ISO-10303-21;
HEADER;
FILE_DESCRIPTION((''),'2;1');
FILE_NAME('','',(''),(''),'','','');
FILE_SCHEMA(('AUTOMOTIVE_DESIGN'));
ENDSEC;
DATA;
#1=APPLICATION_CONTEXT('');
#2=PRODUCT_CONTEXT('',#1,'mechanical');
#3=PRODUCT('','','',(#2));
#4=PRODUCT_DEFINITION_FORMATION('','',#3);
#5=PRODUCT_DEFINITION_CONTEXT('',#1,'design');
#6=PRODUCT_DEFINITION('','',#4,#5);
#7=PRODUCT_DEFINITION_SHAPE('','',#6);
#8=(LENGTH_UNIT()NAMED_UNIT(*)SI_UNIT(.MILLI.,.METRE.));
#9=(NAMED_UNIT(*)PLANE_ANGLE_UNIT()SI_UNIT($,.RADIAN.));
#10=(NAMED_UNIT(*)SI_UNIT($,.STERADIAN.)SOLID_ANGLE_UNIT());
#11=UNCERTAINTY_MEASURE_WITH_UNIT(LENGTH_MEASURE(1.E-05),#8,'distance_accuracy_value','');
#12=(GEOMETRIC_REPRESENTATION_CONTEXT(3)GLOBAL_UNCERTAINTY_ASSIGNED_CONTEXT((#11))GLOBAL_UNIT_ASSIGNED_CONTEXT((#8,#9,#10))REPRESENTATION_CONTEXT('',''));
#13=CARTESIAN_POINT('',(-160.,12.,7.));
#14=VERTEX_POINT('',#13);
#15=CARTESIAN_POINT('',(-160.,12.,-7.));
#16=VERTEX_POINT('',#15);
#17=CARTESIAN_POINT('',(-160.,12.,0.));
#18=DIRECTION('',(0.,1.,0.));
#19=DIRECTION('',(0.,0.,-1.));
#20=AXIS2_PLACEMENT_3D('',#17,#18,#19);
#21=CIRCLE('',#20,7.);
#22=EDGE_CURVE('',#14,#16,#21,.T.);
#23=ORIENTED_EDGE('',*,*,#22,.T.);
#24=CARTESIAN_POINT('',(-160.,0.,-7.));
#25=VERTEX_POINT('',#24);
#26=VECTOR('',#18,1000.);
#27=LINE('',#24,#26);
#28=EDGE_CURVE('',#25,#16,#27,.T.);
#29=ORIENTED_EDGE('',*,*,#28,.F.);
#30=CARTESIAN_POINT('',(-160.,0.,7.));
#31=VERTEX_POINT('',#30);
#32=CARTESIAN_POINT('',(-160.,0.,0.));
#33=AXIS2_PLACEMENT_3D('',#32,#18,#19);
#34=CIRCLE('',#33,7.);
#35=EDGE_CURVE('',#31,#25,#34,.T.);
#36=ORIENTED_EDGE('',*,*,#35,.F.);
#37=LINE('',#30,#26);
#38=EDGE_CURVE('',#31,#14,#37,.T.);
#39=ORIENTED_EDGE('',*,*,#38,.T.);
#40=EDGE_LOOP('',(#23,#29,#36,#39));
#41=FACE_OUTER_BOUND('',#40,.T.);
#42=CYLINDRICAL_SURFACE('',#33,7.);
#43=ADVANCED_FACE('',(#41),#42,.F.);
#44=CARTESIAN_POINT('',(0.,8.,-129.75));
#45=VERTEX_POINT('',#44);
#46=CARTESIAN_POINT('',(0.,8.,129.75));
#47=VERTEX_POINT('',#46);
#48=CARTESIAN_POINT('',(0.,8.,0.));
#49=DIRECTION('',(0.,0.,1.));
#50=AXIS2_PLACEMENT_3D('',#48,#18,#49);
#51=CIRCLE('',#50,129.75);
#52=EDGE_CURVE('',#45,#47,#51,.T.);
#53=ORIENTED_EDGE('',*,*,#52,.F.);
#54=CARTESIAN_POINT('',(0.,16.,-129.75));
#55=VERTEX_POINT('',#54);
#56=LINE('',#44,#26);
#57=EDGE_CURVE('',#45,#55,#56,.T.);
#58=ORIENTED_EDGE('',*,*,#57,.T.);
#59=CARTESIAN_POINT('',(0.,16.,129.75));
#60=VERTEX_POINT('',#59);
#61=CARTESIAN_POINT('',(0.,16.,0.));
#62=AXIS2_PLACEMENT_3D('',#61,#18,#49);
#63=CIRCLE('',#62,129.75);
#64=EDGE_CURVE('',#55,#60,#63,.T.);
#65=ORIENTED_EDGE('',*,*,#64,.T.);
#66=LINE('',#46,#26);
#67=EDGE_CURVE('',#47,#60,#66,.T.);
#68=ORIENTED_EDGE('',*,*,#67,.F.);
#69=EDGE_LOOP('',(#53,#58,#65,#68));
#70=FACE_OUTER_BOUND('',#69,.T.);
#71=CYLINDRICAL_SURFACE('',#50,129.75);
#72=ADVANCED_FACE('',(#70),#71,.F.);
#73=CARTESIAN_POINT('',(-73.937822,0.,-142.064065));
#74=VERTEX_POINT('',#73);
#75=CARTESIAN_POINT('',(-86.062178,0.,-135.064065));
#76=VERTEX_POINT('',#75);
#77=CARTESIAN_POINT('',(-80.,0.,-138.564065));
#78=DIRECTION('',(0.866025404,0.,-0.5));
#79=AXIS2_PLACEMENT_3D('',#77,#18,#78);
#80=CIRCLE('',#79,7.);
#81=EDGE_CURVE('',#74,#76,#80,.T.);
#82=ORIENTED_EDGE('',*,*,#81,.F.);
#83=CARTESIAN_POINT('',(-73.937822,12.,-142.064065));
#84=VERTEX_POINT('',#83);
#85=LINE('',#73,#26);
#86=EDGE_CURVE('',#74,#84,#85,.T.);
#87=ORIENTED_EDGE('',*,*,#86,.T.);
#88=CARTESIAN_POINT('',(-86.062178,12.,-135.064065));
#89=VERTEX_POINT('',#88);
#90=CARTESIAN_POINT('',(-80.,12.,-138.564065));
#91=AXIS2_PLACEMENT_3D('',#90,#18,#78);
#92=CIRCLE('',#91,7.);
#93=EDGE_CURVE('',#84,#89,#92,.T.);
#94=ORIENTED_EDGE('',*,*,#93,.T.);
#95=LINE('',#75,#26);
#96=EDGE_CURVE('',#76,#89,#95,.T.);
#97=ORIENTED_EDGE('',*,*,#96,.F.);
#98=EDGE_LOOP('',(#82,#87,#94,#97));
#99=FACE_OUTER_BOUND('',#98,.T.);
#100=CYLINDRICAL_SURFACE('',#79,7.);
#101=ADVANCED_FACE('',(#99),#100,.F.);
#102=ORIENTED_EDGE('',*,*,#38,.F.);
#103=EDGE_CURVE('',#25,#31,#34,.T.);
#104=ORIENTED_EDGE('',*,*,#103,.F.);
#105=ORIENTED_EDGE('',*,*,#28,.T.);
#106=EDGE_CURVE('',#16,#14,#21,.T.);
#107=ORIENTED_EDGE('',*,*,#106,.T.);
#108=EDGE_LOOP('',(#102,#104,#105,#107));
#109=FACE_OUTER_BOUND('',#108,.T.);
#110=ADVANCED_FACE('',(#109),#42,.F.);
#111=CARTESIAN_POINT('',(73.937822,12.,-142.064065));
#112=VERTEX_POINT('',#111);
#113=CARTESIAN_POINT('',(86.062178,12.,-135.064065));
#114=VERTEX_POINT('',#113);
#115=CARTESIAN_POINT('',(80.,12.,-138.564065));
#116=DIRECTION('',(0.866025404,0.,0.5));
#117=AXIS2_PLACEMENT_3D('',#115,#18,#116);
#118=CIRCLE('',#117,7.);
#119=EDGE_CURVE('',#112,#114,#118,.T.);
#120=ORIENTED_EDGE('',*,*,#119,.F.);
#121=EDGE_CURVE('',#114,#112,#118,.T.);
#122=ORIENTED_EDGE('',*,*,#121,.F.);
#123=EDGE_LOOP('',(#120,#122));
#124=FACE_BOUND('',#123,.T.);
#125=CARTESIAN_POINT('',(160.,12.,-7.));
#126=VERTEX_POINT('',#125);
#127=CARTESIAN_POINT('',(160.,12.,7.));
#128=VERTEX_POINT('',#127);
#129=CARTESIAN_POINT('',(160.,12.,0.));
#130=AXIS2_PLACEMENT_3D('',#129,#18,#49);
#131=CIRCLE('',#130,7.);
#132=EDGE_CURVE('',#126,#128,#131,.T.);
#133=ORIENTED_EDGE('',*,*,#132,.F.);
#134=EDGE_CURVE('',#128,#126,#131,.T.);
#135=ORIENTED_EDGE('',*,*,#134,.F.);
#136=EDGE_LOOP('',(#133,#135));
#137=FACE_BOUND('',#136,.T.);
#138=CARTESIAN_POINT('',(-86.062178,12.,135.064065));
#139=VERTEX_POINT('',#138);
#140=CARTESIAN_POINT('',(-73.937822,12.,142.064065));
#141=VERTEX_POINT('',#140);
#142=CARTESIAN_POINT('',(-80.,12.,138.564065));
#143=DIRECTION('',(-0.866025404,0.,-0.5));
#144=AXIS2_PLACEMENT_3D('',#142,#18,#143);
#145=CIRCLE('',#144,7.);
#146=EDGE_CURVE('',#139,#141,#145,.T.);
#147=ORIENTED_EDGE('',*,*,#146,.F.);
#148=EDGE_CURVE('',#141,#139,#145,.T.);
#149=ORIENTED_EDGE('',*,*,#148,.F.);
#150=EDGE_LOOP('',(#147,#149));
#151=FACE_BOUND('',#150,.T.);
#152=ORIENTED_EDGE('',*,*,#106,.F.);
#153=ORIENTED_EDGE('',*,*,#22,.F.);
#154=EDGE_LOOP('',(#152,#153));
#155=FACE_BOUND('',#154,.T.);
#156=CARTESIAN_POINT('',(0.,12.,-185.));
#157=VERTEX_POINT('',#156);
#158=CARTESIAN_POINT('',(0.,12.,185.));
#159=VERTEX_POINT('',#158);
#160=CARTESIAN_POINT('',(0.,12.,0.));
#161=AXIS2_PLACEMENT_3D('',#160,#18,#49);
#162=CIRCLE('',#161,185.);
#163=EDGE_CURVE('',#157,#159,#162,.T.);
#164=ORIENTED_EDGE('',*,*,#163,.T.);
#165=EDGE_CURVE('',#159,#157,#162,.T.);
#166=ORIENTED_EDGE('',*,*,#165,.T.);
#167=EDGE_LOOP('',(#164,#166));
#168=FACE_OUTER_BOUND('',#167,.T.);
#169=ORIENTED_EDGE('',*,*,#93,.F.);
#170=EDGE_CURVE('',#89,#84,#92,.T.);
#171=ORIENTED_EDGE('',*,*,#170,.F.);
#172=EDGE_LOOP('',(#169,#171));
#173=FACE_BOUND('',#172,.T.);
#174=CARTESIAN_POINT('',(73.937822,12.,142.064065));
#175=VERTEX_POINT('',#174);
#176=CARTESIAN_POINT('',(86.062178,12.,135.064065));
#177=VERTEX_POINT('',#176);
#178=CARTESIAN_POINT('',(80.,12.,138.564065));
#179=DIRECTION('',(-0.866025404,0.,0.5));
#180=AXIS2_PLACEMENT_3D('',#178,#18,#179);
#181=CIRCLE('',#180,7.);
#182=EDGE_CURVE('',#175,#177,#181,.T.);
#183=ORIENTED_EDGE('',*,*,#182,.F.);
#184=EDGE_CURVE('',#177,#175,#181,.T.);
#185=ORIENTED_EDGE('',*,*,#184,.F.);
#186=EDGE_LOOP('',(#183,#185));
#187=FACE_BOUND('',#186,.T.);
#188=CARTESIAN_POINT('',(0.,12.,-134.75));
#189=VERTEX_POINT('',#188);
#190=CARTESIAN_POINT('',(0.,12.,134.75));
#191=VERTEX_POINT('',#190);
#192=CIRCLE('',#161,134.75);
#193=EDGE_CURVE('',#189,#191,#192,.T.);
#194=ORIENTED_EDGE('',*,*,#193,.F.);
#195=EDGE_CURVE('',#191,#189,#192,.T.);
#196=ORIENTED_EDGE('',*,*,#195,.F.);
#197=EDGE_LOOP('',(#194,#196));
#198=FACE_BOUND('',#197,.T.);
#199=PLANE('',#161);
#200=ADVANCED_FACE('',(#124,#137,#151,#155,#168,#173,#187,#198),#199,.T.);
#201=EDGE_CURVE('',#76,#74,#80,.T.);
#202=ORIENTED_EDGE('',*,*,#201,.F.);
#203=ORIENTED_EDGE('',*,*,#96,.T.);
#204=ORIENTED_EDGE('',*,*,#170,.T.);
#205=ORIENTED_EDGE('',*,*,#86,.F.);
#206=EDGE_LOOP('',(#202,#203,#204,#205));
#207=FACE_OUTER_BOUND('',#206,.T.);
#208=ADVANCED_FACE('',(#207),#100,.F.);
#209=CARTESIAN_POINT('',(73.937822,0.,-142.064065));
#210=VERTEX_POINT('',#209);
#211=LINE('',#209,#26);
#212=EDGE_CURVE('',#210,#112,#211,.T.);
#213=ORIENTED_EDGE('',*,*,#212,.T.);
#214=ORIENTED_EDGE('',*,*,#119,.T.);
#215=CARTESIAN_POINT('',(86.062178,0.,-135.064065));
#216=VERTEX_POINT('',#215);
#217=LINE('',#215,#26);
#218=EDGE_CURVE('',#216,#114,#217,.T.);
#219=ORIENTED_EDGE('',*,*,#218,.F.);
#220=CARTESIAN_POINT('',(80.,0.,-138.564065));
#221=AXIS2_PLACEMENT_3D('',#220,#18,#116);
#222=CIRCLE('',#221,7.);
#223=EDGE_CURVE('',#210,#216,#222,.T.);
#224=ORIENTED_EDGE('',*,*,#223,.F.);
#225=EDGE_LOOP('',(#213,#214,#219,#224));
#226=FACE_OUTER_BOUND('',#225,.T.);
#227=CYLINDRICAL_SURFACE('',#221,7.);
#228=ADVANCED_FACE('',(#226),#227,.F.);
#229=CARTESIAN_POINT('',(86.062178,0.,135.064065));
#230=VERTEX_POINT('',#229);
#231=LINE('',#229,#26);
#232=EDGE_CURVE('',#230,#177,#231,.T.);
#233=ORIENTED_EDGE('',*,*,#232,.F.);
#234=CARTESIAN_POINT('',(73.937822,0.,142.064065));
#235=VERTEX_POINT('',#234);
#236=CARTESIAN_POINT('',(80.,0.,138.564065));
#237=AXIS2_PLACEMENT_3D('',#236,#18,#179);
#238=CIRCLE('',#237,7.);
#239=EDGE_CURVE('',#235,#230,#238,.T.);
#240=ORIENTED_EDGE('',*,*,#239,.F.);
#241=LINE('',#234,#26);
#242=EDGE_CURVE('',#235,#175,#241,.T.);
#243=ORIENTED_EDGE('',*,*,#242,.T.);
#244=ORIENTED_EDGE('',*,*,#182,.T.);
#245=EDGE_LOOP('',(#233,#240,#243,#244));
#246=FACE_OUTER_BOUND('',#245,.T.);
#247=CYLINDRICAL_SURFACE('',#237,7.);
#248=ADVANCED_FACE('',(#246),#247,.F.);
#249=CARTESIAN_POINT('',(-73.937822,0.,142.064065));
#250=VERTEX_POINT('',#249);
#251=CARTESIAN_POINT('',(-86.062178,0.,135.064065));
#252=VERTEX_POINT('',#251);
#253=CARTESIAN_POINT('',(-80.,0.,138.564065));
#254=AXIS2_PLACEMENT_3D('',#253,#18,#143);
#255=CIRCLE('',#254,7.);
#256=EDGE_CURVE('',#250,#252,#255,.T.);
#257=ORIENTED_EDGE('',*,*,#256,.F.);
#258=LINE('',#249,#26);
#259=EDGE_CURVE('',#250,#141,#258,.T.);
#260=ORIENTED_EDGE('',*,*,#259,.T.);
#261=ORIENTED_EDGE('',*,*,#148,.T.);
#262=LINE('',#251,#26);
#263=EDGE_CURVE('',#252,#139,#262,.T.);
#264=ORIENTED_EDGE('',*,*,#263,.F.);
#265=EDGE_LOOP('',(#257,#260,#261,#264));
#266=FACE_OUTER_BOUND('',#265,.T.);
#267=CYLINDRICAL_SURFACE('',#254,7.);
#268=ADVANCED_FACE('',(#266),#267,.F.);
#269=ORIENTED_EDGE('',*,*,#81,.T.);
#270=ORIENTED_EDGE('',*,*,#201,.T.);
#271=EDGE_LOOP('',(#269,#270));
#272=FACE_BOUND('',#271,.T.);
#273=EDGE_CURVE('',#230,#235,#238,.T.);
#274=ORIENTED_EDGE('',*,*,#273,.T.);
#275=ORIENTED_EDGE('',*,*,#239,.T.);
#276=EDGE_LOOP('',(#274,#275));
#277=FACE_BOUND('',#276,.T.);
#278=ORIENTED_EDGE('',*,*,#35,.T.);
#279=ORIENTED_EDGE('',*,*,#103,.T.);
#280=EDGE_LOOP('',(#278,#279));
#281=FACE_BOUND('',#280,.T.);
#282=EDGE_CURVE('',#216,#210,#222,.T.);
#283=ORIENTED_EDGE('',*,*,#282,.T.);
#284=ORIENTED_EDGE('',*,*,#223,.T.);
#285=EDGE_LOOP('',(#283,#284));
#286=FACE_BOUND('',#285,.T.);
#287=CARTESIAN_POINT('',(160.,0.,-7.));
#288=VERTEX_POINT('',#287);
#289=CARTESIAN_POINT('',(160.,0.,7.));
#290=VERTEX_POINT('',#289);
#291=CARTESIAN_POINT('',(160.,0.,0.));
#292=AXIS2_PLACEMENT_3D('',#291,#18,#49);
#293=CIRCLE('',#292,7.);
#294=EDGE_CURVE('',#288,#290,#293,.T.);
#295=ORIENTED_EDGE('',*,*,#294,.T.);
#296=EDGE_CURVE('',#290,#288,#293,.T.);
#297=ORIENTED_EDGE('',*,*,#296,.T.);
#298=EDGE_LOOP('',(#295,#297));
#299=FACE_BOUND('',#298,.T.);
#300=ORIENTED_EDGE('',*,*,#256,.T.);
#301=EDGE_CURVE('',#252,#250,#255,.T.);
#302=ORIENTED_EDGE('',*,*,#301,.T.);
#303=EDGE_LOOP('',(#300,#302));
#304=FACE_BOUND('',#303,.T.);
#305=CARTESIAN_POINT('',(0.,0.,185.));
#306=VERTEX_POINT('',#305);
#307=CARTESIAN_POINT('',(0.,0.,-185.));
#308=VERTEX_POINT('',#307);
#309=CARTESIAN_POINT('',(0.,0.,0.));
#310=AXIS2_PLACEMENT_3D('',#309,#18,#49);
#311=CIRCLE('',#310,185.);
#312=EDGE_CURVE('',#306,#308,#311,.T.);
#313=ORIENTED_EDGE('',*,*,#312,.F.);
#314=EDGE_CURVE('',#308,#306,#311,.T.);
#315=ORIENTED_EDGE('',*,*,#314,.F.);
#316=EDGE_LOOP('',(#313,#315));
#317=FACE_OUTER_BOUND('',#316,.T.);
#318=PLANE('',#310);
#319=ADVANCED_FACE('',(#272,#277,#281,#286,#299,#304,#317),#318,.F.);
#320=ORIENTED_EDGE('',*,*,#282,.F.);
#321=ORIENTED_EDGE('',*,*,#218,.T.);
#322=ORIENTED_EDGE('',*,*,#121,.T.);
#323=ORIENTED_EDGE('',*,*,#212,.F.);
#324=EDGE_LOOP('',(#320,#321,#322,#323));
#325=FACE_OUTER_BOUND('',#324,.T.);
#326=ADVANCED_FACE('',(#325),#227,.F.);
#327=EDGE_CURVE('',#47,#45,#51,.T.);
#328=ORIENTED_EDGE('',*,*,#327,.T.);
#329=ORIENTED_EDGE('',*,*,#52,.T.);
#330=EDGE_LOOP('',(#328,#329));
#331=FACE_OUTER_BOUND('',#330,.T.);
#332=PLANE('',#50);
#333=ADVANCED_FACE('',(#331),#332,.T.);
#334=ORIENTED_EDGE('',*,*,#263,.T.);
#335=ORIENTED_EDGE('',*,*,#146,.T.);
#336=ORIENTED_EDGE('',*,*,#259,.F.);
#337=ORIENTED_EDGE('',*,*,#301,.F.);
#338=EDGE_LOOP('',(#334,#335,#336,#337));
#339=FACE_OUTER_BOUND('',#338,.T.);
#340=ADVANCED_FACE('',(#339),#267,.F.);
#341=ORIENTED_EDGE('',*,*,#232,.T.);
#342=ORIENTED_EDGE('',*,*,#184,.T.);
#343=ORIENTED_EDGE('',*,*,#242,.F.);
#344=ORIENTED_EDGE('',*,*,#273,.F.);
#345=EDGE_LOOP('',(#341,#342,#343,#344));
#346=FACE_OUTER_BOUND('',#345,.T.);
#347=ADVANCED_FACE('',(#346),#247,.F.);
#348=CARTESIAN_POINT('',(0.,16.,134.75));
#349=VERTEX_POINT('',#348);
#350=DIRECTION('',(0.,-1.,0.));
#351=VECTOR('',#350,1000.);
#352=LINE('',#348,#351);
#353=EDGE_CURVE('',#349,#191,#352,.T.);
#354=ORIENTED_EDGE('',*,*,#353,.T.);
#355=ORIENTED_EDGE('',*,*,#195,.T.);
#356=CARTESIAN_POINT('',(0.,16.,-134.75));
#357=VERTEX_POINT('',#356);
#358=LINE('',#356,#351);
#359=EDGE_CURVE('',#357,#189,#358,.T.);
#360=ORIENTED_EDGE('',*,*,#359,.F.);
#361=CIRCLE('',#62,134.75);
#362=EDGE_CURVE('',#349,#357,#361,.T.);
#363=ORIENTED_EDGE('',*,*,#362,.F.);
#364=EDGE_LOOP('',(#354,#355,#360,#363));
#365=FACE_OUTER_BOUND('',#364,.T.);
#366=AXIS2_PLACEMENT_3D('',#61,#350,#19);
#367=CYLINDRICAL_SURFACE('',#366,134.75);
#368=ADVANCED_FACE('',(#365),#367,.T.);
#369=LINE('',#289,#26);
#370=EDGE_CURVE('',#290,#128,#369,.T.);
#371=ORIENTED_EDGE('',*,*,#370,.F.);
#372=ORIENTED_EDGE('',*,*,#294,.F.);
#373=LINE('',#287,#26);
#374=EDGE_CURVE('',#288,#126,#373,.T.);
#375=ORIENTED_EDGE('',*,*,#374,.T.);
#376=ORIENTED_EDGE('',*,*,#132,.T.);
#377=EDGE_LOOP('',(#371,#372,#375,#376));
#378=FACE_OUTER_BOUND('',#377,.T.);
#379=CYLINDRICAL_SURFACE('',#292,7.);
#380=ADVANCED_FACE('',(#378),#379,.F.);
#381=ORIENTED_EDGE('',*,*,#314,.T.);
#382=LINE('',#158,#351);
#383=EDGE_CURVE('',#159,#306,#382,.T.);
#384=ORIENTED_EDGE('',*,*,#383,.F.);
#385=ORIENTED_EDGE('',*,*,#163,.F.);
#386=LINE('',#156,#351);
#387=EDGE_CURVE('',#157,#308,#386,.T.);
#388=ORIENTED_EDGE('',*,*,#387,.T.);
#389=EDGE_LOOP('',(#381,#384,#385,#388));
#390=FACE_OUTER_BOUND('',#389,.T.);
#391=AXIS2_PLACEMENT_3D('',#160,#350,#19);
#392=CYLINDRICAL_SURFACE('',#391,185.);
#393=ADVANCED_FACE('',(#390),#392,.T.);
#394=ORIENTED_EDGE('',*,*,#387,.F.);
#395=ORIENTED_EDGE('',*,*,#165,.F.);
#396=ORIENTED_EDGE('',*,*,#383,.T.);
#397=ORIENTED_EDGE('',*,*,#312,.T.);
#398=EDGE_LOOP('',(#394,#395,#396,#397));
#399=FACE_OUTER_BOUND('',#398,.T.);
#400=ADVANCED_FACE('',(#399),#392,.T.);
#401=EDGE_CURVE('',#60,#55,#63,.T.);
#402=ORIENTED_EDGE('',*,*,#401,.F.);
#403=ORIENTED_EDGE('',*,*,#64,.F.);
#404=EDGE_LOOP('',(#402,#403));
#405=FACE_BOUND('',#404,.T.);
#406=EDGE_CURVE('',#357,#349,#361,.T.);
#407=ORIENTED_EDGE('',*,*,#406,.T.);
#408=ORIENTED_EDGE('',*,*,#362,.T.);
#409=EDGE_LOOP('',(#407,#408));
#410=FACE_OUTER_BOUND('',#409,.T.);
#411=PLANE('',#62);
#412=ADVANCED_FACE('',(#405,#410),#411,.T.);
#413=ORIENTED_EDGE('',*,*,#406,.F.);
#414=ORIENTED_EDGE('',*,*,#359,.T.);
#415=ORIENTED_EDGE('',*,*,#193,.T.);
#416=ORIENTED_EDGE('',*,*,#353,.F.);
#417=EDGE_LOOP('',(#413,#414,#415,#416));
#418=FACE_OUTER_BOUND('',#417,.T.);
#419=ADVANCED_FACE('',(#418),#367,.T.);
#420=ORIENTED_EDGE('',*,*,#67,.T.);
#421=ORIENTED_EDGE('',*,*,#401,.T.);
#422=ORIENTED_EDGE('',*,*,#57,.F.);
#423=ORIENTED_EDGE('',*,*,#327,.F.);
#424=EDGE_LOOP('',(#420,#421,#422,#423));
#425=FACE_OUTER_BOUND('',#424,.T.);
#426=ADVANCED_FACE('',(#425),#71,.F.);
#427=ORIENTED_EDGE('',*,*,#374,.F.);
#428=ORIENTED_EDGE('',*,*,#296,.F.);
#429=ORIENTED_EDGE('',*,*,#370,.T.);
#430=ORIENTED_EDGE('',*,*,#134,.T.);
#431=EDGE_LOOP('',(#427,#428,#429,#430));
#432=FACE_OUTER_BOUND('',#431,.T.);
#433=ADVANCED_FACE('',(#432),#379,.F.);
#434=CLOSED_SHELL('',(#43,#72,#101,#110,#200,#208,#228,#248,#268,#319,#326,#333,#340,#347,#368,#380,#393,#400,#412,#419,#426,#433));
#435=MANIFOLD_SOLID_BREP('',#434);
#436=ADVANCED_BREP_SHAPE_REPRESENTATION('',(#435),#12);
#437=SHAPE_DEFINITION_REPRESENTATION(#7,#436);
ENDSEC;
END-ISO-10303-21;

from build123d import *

# Parameters (mm, degrees)
SKETCH1_R           = 185
BOSS_EXTRUDE1_DEPTH = 12
SKETCH2_R           = 129.75
CUT_EXTRUDE1_DEPTH  = 4
BOSS_EXTRUDE2_START = 4
SKETCH3_R           = 134.75
SKETCH3_R_2         = 129.75
BOSS_EXTRUDE2_DEPTH = 4
SKETCH5_R           = 7
CUT_EXTRUDE3_DEPTH  = 262.90456277
CIRPATTERN2_COUNT   = 6


with BuildPart() as part:
    # Sketch1 → Boss-Extrude1 (new body)
    with BuildSketch(Plane(origin=(0, 0, 0), x_dir=(1, 0, 0), z_dir=(0, 1, 0))):
        with Locations(Location((0, 0, 0), (0, 0, 270))):
            Circle(SKETCH1_R)
    extrude(amount=BOSS_EXTRUDE1_DEPTH)

    # Sketch2 → Cut-Extrude1 (cut)
    with BuildSketch(Plane(origin=(0, 12, 0), x_dir=(1, 0, 0), z_dir=(0, 1, 0))):
        with Locations(Location((0, 0, 0), (0, 0, 270))):
            Circle(SKETCH2_R)
    extrude(amount=-CUT_EXTRUDE1_DEPTH, mode=Mode.SUBTRACT)

    # Sketch3 → Boss-Extrude2 (add)
    with BuildSketch(Plane(origin=(0, 12, 0), x_dir=(1, 0, 0), z_dir=(0, 1, 0)).offset(BOSS_EXTRUDE2_START)):
        with Locations(Location((0, 0, 0), (0, 0, 270))):
            Circle(SKETCH3_R)
        with Locations(Location((0, 0, 0), (0, 0, 270))):
            Circle(SKETCH3_R_2, mode=Mode.SUBTRACT)
    extrude(amount=-BOSS_EXTRUDE2_DEPTH)

    # Sketch5 → Cut-Extrude3 (cut, through all)
    with BuildSketch(Plane(origin=(0, 12, 0), x_dir=(1, 0, 0), z_dir=(0, 1, 0))):
        with Locations(Location((160, 0, 0), (0, 0, 270))):
            Circle(SKETCH5_R)
    cut_extrude3 = extrude(amount=-CUT_EXTRUDE3_DEPTH, mode=Mode.SUBTRACT)

    # CirPattern2: Cut-Extrude3 ×6 about axis
    cirpattern2_axis = Axis((0, 0, 0), (0, 1, 0))
    for i in range(1, CIRPATTERN2_COUNT):
        add(cut_extrude3.rotate(cirpattern2_axis, i * 360 / CIRPATTERN2_COUNT), mode=Mode.SUBTRACT)


solid = part.part
